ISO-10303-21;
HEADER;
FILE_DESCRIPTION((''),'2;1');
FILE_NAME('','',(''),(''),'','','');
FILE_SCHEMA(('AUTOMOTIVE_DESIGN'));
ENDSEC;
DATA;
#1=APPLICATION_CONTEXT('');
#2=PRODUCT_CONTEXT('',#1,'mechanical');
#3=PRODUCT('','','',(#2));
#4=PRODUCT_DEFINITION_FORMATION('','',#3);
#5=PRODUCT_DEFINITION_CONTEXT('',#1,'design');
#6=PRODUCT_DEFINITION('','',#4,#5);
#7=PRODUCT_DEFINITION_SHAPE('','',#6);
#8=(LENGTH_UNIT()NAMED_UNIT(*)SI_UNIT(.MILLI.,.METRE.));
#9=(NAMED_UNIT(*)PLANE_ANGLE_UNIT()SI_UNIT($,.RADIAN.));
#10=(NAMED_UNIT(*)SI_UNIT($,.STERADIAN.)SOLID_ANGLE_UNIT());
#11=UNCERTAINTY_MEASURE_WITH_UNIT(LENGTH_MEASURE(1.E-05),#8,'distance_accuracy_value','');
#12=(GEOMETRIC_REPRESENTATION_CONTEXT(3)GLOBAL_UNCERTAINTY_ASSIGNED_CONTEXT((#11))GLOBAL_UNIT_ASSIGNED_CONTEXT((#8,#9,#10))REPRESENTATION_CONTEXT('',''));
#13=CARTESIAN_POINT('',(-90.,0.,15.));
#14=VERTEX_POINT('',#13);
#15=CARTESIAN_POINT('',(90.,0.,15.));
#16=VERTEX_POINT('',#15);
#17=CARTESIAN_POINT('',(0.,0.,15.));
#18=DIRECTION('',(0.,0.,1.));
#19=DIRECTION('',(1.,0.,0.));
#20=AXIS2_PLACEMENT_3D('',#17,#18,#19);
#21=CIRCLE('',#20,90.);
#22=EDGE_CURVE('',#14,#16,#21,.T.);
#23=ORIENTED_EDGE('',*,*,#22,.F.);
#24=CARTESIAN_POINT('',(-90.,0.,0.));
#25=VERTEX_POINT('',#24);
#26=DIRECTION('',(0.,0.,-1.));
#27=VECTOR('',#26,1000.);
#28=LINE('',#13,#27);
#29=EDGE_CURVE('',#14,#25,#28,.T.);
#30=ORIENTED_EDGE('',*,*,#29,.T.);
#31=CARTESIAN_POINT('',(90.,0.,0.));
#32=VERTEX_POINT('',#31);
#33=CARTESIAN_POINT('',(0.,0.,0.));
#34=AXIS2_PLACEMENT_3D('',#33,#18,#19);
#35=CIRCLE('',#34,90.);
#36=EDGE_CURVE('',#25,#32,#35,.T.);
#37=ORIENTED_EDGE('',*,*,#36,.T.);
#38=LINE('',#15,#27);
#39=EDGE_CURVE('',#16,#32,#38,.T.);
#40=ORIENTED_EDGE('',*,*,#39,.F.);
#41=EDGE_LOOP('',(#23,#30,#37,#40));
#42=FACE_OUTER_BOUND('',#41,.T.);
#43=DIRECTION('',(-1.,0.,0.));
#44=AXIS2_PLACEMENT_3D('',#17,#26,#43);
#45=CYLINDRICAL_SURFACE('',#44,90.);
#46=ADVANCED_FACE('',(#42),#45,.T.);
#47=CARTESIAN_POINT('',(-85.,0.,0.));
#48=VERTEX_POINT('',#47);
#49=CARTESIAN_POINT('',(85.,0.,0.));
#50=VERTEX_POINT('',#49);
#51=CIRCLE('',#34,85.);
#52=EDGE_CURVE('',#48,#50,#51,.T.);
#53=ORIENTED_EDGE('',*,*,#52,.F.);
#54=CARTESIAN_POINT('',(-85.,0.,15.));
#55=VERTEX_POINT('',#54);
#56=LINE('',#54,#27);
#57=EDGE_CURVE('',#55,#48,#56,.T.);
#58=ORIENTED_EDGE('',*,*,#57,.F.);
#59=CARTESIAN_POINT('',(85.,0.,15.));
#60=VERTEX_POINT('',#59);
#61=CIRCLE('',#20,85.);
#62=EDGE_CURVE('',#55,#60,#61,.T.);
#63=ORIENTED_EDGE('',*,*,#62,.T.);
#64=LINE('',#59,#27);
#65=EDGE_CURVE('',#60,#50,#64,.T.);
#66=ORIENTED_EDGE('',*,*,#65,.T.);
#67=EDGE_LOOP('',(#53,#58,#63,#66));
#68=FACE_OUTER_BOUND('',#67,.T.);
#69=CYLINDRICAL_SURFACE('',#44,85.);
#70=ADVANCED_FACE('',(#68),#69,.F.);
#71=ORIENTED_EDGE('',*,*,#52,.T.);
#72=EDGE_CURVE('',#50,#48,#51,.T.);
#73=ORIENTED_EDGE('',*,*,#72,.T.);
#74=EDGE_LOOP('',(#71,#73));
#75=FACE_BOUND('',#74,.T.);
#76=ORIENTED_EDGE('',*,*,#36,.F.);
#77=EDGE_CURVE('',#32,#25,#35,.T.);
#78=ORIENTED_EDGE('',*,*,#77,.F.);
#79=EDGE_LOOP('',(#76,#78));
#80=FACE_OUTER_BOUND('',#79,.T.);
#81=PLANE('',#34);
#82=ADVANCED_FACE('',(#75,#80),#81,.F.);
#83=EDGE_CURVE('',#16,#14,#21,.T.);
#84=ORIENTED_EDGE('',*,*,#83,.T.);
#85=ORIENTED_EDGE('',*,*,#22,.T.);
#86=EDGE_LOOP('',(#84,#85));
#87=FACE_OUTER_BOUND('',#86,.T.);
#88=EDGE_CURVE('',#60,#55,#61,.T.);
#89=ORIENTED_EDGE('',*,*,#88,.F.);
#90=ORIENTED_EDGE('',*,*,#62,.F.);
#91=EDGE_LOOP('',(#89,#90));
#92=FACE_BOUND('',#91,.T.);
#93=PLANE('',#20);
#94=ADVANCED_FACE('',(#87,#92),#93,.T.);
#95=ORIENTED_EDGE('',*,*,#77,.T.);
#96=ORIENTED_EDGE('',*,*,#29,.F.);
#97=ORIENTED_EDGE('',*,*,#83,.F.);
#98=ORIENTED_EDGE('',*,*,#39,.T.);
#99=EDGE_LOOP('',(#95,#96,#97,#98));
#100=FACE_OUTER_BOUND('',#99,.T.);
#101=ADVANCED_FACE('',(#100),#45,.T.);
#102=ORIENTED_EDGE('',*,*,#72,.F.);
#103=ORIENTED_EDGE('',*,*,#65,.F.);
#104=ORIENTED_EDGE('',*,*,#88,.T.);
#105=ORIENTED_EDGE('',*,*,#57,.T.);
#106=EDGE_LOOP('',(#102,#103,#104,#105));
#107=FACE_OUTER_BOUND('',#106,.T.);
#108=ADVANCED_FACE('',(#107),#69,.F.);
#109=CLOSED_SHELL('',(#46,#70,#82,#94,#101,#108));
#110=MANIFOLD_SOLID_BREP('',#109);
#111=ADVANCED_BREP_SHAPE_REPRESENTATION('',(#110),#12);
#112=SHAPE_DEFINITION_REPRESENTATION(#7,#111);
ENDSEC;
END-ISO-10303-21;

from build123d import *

# Parameters (mm, degrees)
SKETCH2_R           = 90
SKETCH2_R_2         = 85
BOSS_EXTRUDE1_DEPTH = 15


with BuildPart() as part:
    # Sketch2 → Boss-Extrude1 (new body)
    with BuildSketch(Plane.XY):
        Circle(SKETCH2_R)
        Circle(SKETCH2_R_2, mode=Mode.SUBTRACT)
    extrude(amount=BOSS_EXTRUDE1_DEPTH)


solid = part.part
